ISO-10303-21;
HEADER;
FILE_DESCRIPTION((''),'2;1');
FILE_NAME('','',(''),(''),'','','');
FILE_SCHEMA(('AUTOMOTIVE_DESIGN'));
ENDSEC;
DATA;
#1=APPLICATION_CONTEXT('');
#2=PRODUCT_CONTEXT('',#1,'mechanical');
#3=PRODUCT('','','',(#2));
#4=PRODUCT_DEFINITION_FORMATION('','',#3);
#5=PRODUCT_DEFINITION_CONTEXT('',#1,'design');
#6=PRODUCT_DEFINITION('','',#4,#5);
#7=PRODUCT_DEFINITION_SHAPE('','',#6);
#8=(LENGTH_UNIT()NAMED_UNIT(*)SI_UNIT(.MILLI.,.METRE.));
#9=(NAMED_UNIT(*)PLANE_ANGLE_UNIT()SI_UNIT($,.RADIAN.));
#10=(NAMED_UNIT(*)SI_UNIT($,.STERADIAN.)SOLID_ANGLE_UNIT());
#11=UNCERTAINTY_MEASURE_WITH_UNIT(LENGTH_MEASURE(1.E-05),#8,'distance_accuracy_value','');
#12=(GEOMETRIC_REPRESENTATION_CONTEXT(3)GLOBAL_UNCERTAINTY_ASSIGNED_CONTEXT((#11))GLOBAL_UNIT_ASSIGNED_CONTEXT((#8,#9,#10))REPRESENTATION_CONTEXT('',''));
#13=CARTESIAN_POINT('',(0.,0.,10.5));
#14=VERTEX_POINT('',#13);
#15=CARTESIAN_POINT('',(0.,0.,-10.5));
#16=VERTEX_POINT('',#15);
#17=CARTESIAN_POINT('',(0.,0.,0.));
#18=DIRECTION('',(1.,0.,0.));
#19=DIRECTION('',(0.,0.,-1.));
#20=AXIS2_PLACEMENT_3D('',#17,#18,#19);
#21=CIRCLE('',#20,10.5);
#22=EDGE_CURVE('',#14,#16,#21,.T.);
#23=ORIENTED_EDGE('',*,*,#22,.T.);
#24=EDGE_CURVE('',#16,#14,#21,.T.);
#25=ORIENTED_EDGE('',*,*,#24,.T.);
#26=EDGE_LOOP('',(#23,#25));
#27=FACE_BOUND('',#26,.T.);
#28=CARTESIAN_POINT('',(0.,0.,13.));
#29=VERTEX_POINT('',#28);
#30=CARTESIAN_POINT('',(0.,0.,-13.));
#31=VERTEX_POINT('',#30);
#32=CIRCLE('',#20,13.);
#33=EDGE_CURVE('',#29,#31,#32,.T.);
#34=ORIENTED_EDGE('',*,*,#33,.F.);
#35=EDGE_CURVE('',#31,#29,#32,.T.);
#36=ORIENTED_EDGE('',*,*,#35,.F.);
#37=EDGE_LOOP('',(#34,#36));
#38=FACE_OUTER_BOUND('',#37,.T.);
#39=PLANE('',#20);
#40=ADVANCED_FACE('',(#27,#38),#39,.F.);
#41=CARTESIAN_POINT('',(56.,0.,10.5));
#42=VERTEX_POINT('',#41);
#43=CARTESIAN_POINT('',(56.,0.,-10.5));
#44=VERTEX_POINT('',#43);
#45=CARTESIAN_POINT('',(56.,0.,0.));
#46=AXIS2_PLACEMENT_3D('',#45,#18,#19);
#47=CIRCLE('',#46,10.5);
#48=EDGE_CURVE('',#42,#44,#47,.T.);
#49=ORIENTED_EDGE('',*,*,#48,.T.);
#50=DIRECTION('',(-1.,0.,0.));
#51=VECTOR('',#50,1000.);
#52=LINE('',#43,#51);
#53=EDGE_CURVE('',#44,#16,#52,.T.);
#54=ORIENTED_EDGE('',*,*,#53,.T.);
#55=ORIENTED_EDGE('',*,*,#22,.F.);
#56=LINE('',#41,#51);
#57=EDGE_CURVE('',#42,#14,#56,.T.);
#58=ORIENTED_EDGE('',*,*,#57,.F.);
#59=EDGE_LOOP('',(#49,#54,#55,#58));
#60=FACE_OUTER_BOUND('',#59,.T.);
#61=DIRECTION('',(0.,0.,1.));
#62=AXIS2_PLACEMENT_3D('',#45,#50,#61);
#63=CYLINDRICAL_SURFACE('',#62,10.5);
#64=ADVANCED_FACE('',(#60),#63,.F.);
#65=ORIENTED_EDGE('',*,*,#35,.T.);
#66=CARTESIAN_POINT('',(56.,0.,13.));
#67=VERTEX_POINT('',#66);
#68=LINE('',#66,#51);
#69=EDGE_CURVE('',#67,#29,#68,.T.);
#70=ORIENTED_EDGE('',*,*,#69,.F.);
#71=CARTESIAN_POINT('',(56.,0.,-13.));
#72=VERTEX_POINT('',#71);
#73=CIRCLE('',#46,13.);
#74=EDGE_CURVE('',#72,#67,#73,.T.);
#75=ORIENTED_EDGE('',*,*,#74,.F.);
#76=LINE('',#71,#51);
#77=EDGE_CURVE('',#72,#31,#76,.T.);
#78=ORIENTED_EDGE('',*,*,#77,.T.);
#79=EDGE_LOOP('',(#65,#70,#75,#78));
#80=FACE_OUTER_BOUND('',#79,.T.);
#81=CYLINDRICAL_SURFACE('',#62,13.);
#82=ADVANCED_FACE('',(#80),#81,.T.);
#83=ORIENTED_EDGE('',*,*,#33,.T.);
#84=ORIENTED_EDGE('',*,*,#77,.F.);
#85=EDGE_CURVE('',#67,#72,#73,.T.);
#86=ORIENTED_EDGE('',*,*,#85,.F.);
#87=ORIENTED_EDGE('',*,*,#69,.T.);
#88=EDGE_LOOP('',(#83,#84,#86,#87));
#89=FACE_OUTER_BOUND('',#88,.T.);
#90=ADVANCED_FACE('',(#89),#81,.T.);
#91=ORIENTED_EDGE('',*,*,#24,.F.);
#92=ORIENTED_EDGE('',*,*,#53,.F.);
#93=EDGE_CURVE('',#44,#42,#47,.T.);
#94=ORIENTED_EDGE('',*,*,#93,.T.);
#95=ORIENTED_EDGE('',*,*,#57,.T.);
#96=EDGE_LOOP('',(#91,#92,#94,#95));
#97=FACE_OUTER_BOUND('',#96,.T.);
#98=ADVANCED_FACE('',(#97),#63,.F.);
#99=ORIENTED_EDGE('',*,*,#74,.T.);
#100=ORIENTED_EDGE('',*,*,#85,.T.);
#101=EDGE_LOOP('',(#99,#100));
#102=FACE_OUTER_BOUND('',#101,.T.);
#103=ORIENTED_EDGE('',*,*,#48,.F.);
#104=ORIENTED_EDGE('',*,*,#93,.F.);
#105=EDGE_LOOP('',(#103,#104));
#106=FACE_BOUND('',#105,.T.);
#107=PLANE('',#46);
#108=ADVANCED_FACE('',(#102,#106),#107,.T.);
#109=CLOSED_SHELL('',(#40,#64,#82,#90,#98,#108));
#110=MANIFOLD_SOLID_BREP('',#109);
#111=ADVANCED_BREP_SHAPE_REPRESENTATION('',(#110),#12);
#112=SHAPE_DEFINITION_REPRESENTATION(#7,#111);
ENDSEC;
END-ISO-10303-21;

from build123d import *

# Parameters (mm, degrees)
SKETCH1_R           = 13
SKETCH1_R_2         = 10.5
BOSS_EXTRUDE1_DEPTH = 56


with BuildPart() as part:
    # Sketch1 → Boss-Extrude1 (new body)
    with BuildSketch(Plane(origin=(0, 0, 0), x_dir=(0, 0, -1), z_dir=(1, 0, 0))):
        Circle(SKETCH1_R)
        Circle(SKETCH1_R_2, mode=Mode.SUBTRACT)
    extrude(amount=BOSS_EXTRUDE1_DEPTH)


solid = part.part
